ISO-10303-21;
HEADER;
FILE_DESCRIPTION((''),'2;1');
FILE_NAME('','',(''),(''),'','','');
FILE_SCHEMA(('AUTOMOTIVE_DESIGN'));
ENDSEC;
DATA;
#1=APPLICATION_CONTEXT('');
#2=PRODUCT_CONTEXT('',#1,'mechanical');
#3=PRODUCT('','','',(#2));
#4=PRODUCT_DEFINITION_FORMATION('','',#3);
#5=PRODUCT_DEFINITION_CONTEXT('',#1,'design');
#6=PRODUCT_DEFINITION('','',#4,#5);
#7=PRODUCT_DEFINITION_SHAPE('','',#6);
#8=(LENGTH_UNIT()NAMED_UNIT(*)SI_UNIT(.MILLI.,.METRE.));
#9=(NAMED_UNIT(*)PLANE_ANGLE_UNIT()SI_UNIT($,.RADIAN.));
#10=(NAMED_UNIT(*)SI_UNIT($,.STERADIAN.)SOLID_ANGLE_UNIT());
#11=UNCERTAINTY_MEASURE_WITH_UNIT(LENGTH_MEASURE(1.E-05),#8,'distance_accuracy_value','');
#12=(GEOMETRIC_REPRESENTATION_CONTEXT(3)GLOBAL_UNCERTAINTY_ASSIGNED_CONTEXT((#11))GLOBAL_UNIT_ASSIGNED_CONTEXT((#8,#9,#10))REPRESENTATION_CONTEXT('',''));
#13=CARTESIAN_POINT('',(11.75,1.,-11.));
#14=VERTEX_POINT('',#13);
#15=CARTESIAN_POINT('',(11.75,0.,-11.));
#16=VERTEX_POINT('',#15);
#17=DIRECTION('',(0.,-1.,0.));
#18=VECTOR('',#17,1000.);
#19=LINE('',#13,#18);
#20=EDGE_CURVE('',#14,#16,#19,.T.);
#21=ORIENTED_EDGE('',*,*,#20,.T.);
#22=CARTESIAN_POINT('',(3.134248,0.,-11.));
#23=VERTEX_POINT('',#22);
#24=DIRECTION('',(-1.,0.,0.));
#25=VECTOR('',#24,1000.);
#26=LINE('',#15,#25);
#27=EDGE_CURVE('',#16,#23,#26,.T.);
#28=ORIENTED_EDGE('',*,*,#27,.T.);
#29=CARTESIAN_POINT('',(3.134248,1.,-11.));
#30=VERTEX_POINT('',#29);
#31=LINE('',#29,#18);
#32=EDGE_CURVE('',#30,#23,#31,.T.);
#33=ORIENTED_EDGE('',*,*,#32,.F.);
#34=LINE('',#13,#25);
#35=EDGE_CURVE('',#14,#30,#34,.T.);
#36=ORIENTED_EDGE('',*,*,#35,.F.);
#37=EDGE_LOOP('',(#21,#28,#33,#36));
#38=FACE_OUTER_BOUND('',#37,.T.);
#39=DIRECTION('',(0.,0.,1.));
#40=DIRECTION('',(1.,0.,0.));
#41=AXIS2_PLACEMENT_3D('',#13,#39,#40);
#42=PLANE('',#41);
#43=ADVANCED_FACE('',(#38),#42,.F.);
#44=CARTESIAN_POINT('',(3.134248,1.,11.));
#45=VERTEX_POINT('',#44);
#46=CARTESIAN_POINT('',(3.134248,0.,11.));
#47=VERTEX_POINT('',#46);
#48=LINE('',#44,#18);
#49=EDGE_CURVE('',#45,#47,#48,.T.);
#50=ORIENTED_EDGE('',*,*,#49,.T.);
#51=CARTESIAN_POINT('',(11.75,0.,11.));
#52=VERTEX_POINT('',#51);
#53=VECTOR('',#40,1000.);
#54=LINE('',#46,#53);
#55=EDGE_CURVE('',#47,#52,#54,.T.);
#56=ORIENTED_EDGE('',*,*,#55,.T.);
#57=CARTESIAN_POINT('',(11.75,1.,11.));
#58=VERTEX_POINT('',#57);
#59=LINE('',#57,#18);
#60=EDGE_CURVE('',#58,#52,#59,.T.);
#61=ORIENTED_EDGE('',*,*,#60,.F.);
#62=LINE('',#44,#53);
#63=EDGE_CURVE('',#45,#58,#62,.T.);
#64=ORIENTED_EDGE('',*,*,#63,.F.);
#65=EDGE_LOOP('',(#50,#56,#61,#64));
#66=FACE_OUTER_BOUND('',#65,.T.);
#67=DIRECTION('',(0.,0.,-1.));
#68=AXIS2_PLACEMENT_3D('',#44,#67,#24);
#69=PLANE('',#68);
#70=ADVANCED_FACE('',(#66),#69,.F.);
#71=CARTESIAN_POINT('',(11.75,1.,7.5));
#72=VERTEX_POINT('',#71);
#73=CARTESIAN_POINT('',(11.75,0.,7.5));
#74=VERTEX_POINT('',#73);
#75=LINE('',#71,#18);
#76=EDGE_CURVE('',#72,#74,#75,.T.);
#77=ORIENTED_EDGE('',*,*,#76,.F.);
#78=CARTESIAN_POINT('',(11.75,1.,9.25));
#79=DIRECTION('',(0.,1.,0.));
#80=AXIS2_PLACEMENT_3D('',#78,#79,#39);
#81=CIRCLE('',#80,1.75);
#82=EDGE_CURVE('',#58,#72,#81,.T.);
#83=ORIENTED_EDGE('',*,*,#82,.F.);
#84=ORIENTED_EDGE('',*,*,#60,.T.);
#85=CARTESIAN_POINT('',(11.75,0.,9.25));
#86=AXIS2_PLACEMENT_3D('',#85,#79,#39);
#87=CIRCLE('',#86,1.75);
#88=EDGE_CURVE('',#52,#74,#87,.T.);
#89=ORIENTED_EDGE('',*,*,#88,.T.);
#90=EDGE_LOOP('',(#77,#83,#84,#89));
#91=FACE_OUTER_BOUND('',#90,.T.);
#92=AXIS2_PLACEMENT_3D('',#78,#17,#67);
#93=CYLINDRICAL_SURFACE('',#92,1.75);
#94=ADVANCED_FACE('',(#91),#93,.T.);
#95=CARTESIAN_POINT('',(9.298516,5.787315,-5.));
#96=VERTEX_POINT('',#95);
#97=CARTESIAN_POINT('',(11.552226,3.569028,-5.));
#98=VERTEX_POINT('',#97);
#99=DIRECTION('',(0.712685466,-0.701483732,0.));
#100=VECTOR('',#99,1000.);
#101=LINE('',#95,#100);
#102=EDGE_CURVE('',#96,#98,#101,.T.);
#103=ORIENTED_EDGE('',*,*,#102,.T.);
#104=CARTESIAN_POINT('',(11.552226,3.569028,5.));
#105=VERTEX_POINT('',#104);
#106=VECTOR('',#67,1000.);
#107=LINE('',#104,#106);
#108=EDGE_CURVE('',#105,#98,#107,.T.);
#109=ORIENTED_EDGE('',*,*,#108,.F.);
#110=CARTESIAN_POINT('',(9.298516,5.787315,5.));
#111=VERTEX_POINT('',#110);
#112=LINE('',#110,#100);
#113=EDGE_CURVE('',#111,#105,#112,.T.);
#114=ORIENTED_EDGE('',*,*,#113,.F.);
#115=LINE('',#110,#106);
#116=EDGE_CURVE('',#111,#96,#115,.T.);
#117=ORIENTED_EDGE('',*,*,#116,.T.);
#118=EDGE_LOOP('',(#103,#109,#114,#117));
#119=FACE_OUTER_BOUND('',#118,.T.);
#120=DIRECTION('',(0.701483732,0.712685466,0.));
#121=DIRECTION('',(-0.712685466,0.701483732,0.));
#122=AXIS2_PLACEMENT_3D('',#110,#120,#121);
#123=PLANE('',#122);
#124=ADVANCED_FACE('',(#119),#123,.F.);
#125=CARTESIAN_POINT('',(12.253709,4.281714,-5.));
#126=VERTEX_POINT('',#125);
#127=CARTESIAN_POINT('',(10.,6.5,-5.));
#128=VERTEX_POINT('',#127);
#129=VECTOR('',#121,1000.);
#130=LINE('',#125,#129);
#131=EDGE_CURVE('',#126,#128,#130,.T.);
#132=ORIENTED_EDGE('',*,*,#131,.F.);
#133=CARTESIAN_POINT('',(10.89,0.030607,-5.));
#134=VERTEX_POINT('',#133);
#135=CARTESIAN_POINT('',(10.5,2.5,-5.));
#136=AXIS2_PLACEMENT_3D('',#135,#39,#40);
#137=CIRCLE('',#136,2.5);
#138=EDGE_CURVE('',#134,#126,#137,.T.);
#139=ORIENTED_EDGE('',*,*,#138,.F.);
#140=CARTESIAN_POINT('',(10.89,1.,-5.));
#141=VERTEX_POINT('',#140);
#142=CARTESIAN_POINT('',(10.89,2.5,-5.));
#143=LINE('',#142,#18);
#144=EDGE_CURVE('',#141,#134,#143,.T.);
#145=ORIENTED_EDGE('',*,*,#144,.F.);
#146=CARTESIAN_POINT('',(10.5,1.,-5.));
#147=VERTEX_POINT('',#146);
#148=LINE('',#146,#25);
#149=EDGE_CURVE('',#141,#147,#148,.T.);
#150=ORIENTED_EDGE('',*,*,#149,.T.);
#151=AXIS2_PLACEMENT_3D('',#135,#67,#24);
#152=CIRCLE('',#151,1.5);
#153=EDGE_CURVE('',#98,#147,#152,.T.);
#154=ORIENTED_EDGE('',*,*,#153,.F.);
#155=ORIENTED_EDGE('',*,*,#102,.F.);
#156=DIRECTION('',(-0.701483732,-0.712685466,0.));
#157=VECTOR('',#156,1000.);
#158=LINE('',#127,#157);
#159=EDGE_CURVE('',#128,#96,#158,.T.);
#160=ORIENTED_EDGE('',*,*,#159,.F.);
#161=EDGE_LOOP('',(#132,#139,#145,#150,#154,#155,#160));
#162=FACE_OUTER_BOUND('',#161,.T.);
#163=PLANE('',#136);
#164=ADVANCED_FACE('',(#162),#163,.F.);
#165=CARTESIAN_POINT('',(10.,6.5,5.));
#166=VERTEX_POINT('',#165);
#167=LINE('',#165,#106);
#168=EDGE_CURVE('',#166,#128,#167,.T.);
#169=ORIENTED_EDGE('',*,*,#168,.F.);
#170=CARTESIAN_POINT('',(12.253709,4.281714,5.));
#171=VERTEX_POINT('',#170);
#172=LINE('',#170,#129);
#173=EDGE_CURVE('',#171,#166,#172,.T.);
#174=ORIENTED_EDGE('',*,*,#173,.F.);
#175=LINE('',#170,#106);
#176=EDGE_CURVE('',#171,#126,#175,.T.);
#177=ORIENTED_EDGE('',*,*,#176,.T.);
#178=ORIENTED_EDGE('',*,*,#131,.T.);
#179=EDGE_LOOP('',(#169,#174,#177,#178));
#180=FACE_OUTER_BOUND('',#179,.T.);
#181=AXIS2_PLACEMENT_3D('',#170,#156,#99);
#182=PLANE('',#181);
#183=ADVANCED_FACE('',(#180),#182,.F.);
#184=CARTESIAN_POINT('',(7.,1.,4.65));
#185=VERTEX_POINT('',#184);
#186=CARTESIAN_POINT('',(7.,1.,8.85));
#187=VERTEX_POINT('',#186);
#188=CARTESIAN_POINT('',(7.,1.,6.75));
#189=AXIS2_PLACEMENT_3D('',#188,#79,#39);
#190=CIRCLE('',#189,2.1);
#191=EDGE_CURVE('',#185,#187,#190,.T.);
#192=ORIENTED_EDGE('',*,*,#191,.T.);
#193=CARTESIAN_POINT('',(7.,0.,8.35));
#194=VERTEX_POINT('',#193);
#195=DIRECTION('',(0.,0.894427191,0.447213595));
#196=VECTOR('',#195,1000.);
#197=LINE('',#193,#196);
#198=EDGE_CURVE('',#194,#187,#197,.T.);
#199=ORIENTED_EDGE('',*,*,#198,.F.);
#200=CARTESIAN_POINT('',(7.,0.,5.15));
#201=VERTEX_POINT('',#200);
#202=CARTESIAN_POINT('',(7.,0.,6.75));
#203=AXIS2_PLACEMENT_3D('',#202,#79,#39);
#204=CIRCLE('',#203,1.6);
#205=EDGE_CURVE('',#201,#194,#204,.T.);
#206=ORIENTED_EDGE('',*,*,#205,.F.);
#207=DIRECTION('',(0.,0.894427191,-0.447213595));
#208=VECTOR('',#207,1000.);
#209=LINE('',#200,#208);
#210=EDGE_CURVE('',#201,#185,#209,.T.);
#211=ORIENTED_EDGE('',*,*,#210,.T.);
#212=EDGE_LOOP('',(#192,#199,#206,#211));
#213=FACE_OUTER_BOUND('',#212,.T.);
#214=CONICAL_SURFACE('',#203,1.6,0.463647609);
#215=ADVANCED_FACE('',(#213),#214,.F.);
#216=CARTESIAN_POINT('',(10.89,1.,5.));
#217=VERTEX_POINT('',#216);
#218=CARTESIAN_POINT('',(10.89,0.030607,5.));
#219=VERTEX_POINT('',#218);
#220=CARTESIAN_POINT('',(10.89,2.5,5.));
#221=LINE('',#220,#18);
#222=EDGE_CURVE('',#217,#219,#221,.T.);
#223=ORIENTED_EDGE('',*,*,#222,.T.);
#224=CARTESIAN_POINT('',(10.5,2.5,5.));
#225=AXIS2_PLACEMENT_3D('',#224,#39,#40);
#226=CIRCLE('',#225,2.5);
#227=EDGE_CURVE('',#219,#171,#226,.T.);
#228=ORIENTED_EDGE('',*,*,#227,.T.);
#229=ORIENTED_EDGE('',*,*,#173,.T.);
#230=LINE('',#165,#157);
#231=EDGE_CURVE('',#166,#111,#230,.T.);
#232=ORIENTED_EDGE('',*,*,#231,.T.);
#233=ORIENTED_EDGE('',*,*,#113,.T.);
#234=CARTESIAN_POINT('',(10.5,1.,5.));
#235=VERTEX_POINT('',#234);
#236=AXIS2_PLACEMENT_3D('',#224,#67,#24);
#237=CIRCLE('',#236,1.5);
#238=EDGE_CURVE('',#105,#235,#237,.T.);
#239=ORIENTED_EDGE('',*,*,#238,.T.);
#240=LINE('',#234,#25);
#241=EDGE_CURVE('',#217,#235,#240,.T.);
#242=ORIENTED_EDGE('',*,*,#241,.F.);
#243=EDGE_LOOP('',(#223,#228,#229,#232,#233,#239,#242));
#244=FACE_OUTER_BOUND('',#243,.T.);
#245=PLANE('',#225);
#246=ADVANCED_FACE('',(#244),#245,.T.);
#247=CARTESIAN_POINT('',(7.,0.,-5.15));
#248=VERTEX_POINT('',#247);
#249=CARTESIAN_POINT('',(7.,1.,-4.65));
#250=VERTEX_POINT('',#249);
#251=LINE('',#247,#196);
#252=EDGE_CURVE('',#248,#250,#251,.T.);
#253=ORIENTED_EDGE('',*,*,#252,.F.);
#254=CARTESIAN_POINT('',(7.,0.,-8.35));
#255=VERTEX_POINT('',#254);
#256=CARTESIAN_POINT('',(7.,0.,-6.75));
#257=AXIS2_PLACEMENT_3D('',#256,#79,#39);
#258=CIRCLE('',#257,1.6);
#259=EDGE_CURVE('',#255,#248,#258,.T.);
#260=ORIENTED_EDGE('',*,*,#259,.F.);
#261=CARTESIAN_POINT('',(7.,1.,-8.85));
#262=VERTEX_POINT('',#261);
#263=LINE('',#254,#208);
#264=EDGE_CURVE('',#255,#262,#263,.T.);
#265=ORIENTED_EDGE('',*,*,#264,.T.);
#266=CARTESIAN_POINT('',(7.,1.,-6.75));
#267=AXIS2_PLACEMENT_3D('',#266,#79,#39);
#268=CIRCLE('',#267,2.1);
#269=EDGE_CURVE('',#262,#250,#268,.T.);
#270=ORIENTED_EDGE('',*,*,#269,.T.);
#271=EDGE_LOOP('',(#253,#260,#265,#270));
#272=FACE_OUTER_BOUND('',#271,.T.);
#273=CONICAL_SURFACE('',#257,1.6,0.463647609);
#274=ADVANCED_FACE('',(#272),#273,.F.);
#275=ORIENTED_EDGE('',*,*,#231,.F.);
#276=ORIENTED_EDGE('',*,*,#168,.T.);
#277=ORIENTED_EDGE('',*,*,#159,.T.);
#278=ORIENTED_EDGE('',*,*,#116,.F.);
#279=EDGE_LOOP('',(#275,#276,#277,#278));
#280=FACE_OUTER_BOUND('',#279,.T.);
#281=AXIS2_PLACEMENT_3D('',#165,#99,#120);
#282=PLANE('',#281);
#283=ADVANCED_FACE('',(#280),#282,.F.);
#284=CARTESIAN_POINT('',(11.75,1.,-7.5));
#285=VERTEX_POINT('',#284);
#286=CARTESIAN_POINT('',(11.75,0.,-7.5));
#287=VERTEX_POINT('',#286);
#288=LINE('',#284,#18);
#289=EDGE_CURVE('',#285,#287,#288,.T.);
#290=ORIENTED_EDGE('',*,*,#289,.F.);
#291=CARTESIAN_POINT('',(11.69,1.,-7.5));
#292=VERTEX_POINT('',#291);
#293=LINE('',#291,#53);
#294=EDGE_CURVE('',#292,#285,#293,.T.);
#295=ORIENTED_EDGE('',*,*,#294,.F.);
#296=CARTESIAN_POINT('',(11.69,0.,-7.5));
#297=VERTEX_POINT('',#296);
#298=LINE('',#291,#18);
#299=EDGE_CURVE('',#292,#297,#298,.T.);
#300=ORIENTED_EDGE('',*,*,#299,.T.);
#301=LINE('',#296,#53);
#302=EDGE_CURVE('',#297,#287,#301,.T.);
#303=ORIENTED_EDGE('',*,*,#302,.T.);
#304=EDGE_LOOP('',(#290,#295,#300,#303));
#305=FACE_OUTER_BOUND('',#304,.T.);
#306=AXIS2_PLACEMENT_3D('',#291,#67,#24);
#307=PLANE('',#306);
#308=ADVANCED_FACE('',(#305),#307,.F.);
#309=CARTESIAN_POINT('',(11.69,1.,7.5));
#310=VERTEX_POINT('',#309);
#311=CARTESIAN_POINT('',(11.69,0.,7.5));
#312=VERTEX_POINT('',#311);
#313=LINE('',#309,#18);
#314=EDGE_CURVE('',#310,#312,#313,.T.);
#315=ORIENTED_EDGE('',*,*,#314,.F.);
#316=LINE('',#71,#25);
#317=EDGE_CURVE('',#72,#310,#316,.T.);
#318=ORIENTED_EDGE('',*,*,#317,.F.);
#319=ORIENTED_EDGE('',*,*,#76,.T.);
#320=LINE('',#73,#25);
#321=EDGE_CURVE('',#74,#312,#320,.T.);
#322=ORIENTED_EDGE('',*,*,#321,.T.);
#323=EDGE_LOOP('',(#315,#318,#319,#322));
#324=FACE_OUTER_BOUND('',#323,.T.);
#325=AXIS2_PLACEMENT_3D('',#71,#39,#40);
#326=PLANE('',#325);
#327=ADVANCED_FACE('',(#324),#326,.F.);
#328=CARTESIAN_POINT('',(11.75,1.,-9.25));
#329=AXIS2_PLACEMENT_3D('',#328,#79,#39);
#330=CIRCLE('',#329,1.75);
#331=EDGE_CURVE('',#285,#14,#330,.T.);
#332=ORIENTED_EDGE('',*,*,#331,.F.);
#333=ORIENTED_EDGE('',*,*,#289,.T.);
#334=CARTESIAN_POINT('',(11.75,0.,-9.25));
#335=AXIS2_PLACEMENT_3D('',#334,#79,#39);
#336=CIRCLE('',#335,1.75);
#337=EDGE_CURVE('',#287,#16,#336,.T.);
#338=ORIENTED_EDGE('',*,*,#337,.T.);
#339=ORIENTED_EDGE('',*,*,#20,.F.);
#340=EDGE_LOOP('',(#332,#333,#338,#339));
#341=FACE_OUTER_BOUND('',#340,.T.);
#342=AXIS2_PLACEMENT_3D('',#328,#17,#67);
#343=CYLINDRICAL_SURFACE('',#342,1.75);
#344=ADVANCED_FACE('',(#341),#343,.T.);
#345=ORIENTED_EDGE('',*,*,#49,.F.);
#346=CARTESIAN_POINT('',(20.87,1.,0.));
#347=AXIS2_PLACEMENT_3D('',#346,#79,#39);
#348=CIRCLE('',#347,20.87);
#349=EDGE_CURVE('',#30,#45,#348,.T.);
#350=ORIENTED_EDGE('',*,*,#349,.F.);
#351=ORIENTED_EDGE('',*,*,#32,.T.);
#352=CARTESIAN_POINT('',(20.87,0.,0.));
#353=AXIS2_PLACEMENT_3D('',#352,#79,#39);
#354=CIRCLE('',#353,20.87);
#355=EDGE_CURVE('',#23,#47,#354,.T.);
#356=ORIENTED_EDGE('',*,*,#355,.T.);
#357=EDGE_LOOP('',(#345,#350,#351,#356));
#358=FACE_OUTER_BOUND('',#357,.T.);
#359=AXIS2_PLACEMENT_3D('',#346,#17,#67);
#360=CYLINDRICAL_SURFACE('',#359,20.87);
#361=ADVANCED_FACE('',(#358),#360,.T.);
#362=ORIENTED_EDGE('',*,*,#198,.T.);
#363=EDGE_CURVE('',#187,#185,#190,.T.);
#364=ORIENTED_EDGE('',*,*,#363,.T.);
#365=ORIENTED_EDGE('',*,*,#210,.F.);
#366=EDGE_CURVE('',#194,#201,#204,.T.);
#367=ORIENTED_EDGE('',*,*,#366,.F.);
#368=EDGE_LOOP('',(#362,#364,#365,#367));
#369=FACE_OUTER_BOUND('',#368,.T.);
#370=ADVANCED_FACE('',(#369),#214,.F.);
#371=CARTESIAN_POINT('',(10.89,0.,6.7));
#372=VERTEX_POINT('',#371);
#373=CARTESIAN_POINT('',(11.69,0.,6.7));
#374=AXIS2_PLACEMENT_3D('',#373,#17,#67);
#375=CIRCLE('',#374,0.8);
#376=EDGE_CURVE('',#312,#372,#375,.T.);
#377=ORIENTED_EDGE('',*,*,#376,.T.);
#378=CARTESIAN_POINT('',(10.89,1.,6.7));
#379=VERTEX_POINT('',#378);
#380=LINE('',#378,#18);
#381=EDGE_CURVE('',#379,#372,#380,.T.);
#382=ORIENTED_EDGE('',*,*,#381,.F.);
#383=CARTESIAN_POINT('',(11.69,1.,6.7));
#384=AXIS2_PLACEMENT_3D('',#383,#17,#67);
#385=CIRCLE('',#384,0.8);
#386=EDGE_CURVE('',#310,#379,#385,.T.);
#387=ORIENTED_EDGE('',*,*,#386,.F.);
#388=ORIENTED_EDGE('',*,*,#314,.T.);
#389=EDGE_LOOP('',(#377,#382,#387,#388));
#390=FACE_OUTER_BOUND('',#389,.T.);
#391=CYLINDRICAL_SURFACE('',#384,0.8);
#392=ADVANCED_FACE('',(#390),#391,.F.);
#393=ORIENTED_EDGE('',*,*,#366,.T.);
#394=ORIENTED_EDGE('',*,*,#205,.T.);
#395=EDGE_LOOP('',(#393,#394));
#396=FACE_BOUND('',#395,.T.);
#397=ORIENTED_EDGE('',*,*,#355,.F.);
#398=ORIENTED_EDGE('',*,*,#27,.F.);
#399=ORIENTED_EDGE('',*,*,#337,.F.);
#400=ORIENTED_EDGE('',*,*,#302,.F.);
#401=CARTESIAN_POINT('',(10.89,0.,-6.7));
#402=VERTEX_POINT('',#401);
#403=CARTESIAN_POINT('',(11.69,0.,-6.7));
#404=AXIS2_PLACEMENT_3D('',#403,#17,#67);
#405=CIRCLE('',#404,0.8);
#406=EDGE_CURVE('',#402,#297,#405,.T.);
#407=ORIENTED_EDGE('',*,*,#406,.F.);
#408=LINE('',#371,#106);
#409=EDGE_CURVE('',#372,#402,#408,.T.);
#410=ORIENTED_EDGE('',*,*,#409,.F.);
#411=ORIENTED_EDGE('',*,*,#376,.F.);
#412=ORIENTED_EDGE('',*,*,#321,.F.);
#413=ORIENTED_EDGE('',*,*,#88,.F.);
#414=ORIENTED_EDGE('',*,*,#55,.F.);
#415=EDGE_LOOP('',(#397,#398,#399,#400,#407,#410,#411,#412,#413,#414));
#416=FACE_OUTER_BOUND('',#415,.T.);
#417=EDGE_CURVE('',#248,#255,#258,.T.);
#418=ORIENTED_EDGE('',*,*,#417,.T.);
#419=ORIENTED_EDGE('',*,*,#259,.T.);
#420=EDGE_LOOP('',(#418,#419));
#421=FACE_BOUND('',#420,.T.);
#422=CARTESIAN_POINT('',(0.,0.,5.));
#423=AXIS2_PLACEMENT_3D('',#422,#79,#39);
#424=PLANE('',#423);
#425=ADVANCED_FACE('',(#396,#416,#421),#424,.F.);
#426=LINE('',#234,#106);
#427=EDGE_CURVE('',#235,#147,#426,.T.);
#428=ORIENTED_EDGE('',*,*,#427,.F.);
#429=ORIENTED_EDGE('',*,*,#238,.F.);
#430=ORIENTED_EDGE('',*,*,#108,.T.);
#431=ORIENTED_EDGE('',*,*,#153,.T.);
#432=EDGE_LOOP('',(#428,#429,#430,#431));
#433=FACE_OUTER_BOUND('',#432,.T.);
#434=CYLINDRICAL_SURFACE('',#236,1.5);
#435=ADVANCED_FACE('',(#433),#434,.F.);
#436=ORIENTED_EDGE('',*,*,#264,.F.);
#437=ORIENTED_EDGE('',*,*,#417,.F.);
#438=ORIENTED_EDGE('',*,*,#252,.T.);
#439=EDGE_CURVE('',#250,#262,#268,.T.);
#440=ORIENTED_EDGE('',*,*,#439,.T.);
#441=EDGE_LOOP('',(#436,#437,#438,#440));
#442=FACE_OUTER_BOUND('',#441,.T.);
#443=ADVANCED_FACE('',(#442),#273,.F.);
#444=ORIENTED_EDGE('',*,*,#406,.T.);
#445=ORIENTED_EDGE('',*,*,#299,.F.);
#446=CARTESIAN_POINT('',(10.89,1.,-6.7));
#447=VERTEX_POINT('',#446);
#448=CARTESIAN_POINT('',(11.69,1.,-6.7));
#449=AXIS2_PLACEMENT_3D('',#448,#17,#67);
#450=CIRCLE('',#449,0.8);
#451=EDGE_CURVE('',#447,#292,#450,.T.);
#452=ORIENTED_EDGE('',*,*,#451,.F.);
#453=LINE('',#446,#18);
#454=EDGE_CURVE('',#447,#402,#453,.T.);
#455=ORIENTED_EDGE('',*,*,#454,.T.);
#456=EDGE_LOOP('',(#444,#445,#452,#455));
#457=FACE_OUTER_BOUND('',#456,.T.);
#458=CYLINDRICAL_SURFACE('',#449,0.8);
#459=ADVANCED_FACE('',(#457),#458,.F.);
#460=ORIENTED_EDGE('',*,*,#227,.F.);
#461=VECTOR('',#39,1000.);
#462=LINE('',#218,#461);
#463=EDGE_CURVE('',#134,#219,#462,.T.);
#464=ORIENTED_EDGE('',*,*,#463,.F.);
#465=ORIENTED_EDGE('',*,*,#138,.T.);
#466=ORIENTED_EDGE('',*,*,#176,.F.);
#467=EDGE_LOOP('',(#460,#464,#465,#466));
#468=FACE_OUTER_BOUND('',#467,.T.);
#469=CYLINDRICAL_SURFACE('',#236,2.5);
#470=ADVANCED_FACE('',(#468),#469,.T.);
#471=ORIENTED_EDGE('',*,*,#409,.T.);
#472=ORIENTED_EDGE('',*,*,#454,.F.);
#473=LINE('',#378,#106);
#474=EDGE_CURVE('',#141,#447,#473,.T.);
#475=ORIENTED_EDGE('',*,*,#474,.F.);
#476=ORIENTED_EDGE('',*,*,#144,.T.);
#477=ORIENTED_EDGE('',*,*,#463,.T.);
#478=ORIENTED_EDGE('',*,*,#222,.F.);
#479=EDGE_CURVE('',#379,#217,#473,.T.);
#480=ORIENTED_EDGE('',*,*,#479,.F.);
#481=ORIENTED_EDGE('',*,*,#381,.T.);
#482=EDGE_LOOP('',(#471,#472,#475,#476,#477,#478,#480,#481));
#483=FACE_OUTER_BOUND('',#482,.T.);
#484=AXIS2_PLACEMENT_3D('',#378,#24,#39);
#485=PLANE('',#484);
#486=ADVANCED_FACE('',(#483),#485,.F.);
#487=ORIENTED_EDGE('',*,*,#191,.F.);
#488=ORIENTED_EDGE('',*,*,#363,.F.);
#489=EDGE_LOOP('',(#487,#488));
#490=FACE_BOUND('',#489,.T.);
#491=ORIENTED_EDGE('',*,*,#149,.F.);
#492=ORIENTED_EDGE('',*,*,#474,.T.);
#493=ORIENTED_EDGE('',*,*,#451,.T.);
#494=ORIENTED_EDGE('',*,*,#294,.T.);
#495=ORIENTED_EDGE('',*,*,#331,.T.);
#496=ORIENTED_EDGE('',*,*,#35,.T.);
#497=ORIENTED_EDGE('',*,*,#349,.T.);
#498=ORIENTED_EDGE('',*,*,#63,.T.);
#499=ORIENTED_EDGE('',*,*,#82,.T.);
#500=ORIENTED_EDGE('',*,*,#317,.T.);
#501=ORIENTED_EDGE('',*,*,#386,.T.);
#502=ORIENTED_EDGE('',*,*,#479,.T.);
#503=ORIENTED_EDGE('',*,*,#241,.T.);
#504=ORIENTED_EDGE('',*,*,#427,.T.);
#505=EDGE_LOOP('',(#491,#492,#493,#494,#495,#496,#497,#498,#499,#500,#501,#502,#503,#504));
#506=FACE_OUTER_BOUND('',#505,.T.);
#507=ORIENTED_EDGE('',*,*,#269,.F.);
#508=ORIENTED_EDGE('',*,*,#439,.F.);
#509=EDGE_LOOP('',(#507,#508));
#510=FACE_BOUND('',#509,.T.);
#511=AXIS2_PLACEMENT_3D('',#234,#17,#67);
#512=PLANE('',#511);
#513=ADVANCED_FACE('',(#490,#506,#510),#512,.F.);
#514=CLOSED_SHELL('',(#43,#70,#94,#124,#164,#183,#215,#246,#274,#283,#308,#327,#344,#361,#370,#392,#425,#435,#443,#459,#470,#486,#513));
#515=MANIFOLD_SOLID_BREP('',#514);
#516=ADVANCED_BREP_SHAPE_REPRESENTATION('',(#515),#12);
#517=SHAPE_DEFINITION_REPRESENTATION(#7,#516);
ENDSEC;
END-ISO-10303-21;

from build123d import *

# Parameters (mm, degrees)
BOSS_EXTRUDE1_DEPTH      = 5
BOSS_EXTRUDE1_DEPTH_BACK = 5
BOSS_EXTRUDE2_DEPTH      = 1
SKETCH3_W                = 100
SKETCH3_H                = 100
SKETCH3_R                = 20.87
CUT_EXTRUDE1_DEPTH       = 2


with BuildPart() as part:
    # Sketch1 → Boss-Extrude1 (new, two sides: drawn at the far end of the back side and taken through both)
    with BuildSketch(Plane.XY.offset(-BOSS_EXTRUDE1_DEPTH_BACK)):
        with BuildLine():
            Line((0, 0), (10.5, 0))
            ThreePointArc((10.5, 0), (12.813469706, 1.552446351), (12.253709329, 4.281713666))
            Line((12.253709329, 4.281713666), (10, 6.5))
            Line((10, 6.5), (9.298516268, 5.787314534))
            Line((9.298516268, 5.787314534), (11.552225598, 3.5690282))
            ThreePointArc((11.552225598, 3.5690282), (11.888081824, 1.931467811), (10.5, 1))
            Line((10.5, 1), (0, 1))
            Line((0, 1), (0, 0))
        make_face()
    extrude(amount=BOSS_EXTRUDE1_DEPTH + BOSS_EXTRUDE1_DEPTH_BACK)

    # Sketch2 → Boss-Extrude2 (add)
    with BuildSketch(Plane(origin=(0, 0, 0), x_dir=(1, 0, 0), z_dir=(0, 1, 0))):
        with BuildLine():
            Line((3.134247972, -11), (11.75, -11))
            ThreePointArc((11.75, -11), (13.5, -9.25), (11.75, -7.5))
            Line((11.75, -7.5), (11.69, -7.5))
            ThreePointArc((11.69, -7.5), (11.124314575, -7.265685425), (10.89, -6.7))
            Line((10.89, -6.7), (10.89, 6.7))
            ThreePointArc((10.89, 6.7), (11.124314575, 7.265685425), (11.69, 7.5))
            Line((11.69, 7.5), (11.75, 7.5))
            ThreePointArc((11.75, 7.5), (13.5, 9.25), (11.75, 11))
            Line((11.75, 11), (3.134247972, 11))
            ThreePointArc((3.134247972, 11), (0, 0), (3.134247972, -11))
        make_face()
    extrude(amount=BOSS_EXTRUDE2_DEPTH)

    # Sketch3 → Cut-Extrude1 (cut)
    with BuildSketch(Plane(origin=(0, 0, 0), x_dir=(1, 0, 0), z_dir=(0, 1, 0))):
        Rectangle(SKETCH3_W, SKETCH3_H)
        with Locations((20.87, 0)):
            Circle(SKETCH3_R, mode=Mode.SUBTRACT)
    extrude(amount=CUT_EXTRUDE1_DEPTH, mode=Mode.SUBTRACT)

    # Sketch4 → Cut-Revolve1 (revolve, cut)
    with BuildSketch(Plane.XY.offset(6.75), mode=Mode.PRIVATE) as cut_revolve1_sk:
        Polygon((7, 1), (9.1, 1), (8.6, 0), (7, 0), align=None)
    revolve(cut_revolve1_sk.sketch.rotate(Axis((7, 0, 6.75), (0, 1, 0)), 270), axis=Axis((7, 0, 6.75), (0, 1, 0)), mode=Mode.SUBTRACT)

    # Sketch5 → Cut-Revolve2 (revolve, cut)
    with BuildSketch(Plane.XY.offset(-6.75), mode=Mode.PRIVATE) as cut_revolve2_sk:
        Polygon((7, 1), (9.1, 1), (8.6, 0), (7, 0), align=None)
    revolve(cut_revolve2_sk.sketch.rotate(Axis((7, 0, -6.75), (0, 1, 0)), 270), axis=Axis((7, 0, -6.75), (0, 1, 0)), mode=Mode.SUBTRACT)


solid = part.part
